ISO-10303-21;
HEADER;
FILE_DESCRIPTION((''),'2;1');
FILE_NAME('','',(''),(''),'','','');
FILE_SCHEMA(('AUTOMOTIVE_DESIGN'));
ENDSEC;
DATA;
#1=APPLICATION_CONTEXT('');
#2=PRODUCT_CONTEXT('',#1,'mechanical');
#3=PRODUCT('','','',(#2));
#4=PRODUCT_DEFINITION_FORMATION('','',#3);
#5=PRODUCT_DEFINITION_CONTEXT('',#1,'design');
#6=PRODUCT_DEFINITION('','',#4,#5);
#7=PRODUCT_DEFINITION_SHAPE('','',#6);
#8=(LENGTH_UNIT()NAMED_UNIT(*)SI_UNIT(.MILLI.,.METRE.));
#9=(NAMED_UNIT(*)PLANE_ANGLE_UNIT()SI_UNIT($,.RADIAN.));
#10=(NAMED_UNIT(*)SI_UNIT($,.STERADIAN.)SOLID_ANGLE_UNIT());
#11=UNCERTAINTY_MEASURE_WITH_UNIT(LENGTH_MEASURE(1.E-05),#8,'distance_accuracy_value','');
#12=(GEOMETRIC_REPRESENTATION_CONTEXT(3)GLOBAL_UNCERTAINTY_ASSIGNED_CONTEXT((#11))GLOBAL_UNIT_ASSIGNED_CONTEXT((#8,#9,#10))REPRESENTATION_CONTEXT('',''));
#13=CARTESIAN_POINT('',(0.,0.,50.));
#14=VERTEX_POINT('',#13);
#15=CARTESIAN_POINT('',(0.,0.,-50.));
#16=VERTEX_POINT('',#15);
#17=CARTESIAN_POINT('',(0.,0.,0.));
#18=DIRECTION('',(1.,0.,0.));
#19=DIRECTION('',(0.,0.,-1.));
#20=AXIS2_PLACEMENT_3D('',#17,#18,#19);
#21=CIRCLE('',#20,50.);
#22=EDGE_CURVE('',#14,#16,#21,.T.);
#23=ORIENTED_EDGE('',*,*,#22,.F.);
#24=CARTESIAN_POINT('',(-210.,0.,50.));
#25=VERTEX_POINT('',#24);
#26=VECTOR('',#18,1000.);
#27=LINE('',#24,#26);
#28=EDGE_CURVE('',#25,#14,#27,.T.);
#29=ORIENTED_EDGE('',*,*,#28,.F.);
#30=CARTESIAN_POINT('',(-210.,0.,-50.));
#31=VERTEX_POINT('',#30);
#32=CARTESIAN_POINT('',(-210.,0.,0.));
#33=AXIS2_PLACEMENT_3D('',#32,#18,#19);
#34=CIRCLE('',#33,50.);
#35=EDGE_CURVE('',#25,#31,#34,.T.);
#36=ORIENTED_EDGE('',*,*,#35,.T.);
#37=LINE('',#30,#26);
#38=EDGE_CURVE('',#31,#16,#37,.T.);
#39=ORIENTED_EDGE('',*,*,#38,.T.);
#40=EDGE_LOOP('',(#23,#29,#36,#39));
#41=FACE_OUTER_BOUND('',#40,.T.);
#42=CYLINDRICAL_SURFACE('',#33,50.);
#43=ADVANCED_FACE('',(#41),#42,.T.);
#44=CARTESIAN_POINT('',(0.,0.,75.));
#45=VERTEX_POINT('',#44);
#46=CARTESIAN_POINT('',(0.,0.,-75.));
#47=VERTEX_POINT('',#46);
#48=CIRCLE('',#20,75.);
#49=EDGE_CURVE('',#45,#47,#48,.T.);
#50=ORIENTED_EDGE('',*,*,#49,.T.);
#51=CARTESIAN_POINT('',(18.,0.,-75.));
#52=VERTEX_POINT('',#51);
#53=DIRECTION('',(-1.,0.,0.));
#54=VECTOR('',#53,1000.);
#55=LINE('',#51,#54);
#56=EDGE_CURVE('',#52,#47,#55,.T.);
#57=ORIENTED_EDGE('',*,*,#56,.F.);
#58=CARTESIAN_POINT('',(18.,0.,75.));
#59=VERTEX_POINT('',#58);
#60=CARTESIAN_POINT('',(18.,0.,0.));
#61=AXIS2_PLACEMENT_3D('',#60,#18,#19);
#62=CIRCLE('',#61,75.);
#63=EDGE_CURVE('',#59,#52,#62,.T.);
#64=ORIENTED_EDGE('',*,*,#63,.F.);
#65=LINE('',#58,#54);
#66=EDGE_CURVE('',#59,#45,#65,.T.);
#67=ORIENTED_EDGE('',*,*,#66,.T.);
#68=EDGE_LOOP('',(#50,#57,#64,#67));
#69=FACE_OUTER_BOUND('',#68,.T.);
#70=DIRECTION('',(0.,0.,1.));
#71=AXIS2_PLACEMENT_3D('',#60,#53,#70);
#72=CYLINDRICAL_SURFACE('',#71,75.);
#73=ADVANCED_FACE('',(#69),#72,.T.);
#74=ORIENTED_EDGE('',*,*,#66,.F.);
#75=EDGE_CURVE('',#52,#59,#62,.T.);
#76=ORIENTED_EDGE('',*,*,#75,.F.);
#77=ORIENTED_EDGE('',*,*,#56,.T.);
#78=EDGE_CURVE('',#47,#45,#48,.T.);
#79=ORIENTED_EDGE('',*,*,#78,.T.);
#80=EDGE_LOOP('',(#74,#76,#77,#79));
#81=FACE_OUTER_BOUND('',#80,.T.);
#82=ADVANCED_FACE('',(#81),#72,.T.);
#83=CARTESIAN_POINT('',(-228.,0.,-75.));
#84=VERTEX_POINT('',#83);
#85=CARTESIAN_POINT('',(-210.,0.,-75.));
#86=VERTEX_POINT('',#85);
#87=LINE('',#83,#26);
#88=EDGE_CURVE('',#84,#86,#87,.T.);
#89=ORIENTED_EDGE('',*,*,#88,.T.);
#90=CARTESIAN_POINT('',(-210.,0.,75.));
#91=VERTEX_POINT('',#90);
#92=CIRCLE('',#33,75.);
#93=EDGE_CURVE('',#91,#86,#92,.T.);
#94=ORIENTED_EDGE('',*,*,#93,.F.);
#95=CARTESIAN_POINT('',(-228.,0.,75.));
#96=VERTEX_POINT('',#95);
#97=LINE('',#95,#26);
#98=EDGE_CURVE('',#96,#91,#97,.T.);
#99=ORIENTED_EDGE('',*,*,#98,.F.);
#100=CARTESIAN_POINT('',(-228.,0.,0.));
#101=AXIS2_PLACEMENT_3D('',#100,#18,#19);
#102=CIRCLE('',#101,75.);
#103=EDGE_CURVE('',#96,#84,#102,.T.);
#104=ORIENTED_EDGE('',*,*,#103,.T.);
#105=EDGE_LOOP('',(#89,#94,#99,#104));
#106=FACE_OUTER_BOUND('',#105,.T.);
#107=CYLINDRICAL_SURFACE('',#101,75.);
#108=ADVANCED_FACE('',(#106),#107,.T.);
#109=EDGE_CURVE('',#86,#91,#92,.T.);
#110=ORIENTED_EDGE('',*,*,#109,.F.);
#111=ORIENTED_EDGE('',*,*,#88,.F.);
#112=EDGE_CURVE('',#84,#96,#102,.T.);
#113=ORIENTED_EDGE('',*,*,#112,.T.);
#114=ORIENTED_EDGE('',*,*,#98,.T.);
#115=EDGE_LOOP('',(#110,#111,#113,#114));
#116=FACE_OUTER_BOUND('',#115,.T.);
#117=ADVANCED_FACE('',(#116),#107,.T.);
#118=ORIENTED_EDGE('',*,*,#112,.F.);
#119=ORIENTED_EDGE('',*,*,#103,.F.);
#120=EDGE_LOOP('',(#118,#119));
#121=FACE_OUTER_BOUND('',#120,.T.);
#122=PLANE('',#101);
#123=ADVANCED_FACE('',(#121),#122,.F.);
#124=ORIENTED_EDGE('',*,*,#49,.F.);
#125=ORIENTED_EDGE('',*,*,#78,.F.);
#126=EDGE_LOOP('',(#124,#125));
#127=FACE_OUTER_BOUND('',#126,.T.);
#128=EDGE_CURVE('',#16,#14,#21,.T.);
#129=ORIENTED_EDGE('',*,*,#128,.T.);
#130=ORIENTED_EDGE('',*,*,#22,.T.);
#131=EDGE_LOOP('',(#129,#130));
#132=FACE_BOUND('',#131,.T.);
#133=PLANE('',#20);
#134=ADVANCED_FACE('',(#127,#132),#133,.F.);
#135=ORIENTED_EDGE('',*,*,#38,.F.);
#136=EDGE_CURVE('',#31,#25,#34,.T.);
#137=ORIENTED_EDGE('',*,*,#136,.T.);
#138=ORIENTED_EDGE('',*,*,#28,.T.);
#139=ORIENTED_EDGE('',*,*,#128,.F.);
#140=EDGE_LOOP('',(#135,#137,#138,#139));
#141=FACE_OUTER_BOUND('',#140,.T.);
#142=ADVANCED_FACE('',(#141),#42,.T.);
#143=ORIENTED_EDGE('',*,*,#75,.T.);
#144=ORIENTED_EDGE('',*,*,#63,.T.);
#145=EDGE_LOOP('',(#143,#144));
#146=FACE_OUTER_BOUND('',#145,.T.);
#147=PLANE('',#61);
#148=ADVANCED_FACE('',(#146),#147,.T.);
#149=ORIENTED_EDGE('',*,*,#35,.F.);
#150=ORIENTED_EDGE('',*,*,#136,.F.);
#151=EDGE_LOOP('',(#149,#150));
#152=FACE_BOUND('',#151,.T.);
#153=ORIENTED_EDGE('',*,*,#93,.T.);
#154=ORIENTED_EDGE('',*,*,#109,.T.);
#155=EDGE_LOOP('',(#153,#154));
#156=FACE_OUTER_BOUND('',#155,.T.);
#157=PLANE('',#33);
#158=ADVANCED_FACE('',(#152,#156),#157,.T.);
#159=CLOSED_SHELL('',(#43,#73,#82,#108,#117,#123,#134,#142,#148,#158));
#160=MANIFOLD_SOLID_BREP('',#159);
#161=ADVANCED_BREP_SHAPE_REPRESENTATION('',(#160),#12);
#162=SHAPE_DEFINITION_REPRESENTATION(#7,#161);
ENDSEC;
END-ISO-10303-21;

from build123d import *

# Parameters (mm, degrees)
SKETCH_1_4_R        = 75
BOSS_EXTRUDE1_DEPTH = 18
SKETCH_1_3_R        = 50
BOSS_EXTRUDE2_DEPTH = 210
BOSS_EXTRUDE3_START = -228
SKETCH_1_4_2_R      = 75
BOSS_EXTRUDE3_DEPTH = 18


with BuildPart() as part:
    # Sketch 1_4 → Boss-Extrude1 (new body)
    with BuildSketch(Plane(origin=(0, 0, 0), x_dir=(0, 0, -1), z_dir=(1, 0, 0))):
        Circle(SKETCH_1_4_R)
    extrude(amount=BOSS_EXTRUDE1_DEPTH)

    # 草图1<3> → Boss-Extrude2 (add)
    with BuildSketch(Plane(origin=(0, 0, 0), x_dir=(0, 0, -1), z_dir=(1, 0, 0))):
        Circle(SKETCH_1_3_R)
    extrude(amount=-BOSS_EXTRUDE2_DEPTH)

    # Sketch 1_4 2 → Boss-Extrude3 (add)
    with BuildSketch(Plane(origin=(0, 0, 0), x_dir=(0, 0, -1), z_dir=(1, 0, 0)).offset(BOSS_EXTRUDE3_START)):
        Circle(SKETCH_1_4_2_R)
    extrude(amount=BOSS_EXTRUDE3_DEPTH)


solid = part.part
